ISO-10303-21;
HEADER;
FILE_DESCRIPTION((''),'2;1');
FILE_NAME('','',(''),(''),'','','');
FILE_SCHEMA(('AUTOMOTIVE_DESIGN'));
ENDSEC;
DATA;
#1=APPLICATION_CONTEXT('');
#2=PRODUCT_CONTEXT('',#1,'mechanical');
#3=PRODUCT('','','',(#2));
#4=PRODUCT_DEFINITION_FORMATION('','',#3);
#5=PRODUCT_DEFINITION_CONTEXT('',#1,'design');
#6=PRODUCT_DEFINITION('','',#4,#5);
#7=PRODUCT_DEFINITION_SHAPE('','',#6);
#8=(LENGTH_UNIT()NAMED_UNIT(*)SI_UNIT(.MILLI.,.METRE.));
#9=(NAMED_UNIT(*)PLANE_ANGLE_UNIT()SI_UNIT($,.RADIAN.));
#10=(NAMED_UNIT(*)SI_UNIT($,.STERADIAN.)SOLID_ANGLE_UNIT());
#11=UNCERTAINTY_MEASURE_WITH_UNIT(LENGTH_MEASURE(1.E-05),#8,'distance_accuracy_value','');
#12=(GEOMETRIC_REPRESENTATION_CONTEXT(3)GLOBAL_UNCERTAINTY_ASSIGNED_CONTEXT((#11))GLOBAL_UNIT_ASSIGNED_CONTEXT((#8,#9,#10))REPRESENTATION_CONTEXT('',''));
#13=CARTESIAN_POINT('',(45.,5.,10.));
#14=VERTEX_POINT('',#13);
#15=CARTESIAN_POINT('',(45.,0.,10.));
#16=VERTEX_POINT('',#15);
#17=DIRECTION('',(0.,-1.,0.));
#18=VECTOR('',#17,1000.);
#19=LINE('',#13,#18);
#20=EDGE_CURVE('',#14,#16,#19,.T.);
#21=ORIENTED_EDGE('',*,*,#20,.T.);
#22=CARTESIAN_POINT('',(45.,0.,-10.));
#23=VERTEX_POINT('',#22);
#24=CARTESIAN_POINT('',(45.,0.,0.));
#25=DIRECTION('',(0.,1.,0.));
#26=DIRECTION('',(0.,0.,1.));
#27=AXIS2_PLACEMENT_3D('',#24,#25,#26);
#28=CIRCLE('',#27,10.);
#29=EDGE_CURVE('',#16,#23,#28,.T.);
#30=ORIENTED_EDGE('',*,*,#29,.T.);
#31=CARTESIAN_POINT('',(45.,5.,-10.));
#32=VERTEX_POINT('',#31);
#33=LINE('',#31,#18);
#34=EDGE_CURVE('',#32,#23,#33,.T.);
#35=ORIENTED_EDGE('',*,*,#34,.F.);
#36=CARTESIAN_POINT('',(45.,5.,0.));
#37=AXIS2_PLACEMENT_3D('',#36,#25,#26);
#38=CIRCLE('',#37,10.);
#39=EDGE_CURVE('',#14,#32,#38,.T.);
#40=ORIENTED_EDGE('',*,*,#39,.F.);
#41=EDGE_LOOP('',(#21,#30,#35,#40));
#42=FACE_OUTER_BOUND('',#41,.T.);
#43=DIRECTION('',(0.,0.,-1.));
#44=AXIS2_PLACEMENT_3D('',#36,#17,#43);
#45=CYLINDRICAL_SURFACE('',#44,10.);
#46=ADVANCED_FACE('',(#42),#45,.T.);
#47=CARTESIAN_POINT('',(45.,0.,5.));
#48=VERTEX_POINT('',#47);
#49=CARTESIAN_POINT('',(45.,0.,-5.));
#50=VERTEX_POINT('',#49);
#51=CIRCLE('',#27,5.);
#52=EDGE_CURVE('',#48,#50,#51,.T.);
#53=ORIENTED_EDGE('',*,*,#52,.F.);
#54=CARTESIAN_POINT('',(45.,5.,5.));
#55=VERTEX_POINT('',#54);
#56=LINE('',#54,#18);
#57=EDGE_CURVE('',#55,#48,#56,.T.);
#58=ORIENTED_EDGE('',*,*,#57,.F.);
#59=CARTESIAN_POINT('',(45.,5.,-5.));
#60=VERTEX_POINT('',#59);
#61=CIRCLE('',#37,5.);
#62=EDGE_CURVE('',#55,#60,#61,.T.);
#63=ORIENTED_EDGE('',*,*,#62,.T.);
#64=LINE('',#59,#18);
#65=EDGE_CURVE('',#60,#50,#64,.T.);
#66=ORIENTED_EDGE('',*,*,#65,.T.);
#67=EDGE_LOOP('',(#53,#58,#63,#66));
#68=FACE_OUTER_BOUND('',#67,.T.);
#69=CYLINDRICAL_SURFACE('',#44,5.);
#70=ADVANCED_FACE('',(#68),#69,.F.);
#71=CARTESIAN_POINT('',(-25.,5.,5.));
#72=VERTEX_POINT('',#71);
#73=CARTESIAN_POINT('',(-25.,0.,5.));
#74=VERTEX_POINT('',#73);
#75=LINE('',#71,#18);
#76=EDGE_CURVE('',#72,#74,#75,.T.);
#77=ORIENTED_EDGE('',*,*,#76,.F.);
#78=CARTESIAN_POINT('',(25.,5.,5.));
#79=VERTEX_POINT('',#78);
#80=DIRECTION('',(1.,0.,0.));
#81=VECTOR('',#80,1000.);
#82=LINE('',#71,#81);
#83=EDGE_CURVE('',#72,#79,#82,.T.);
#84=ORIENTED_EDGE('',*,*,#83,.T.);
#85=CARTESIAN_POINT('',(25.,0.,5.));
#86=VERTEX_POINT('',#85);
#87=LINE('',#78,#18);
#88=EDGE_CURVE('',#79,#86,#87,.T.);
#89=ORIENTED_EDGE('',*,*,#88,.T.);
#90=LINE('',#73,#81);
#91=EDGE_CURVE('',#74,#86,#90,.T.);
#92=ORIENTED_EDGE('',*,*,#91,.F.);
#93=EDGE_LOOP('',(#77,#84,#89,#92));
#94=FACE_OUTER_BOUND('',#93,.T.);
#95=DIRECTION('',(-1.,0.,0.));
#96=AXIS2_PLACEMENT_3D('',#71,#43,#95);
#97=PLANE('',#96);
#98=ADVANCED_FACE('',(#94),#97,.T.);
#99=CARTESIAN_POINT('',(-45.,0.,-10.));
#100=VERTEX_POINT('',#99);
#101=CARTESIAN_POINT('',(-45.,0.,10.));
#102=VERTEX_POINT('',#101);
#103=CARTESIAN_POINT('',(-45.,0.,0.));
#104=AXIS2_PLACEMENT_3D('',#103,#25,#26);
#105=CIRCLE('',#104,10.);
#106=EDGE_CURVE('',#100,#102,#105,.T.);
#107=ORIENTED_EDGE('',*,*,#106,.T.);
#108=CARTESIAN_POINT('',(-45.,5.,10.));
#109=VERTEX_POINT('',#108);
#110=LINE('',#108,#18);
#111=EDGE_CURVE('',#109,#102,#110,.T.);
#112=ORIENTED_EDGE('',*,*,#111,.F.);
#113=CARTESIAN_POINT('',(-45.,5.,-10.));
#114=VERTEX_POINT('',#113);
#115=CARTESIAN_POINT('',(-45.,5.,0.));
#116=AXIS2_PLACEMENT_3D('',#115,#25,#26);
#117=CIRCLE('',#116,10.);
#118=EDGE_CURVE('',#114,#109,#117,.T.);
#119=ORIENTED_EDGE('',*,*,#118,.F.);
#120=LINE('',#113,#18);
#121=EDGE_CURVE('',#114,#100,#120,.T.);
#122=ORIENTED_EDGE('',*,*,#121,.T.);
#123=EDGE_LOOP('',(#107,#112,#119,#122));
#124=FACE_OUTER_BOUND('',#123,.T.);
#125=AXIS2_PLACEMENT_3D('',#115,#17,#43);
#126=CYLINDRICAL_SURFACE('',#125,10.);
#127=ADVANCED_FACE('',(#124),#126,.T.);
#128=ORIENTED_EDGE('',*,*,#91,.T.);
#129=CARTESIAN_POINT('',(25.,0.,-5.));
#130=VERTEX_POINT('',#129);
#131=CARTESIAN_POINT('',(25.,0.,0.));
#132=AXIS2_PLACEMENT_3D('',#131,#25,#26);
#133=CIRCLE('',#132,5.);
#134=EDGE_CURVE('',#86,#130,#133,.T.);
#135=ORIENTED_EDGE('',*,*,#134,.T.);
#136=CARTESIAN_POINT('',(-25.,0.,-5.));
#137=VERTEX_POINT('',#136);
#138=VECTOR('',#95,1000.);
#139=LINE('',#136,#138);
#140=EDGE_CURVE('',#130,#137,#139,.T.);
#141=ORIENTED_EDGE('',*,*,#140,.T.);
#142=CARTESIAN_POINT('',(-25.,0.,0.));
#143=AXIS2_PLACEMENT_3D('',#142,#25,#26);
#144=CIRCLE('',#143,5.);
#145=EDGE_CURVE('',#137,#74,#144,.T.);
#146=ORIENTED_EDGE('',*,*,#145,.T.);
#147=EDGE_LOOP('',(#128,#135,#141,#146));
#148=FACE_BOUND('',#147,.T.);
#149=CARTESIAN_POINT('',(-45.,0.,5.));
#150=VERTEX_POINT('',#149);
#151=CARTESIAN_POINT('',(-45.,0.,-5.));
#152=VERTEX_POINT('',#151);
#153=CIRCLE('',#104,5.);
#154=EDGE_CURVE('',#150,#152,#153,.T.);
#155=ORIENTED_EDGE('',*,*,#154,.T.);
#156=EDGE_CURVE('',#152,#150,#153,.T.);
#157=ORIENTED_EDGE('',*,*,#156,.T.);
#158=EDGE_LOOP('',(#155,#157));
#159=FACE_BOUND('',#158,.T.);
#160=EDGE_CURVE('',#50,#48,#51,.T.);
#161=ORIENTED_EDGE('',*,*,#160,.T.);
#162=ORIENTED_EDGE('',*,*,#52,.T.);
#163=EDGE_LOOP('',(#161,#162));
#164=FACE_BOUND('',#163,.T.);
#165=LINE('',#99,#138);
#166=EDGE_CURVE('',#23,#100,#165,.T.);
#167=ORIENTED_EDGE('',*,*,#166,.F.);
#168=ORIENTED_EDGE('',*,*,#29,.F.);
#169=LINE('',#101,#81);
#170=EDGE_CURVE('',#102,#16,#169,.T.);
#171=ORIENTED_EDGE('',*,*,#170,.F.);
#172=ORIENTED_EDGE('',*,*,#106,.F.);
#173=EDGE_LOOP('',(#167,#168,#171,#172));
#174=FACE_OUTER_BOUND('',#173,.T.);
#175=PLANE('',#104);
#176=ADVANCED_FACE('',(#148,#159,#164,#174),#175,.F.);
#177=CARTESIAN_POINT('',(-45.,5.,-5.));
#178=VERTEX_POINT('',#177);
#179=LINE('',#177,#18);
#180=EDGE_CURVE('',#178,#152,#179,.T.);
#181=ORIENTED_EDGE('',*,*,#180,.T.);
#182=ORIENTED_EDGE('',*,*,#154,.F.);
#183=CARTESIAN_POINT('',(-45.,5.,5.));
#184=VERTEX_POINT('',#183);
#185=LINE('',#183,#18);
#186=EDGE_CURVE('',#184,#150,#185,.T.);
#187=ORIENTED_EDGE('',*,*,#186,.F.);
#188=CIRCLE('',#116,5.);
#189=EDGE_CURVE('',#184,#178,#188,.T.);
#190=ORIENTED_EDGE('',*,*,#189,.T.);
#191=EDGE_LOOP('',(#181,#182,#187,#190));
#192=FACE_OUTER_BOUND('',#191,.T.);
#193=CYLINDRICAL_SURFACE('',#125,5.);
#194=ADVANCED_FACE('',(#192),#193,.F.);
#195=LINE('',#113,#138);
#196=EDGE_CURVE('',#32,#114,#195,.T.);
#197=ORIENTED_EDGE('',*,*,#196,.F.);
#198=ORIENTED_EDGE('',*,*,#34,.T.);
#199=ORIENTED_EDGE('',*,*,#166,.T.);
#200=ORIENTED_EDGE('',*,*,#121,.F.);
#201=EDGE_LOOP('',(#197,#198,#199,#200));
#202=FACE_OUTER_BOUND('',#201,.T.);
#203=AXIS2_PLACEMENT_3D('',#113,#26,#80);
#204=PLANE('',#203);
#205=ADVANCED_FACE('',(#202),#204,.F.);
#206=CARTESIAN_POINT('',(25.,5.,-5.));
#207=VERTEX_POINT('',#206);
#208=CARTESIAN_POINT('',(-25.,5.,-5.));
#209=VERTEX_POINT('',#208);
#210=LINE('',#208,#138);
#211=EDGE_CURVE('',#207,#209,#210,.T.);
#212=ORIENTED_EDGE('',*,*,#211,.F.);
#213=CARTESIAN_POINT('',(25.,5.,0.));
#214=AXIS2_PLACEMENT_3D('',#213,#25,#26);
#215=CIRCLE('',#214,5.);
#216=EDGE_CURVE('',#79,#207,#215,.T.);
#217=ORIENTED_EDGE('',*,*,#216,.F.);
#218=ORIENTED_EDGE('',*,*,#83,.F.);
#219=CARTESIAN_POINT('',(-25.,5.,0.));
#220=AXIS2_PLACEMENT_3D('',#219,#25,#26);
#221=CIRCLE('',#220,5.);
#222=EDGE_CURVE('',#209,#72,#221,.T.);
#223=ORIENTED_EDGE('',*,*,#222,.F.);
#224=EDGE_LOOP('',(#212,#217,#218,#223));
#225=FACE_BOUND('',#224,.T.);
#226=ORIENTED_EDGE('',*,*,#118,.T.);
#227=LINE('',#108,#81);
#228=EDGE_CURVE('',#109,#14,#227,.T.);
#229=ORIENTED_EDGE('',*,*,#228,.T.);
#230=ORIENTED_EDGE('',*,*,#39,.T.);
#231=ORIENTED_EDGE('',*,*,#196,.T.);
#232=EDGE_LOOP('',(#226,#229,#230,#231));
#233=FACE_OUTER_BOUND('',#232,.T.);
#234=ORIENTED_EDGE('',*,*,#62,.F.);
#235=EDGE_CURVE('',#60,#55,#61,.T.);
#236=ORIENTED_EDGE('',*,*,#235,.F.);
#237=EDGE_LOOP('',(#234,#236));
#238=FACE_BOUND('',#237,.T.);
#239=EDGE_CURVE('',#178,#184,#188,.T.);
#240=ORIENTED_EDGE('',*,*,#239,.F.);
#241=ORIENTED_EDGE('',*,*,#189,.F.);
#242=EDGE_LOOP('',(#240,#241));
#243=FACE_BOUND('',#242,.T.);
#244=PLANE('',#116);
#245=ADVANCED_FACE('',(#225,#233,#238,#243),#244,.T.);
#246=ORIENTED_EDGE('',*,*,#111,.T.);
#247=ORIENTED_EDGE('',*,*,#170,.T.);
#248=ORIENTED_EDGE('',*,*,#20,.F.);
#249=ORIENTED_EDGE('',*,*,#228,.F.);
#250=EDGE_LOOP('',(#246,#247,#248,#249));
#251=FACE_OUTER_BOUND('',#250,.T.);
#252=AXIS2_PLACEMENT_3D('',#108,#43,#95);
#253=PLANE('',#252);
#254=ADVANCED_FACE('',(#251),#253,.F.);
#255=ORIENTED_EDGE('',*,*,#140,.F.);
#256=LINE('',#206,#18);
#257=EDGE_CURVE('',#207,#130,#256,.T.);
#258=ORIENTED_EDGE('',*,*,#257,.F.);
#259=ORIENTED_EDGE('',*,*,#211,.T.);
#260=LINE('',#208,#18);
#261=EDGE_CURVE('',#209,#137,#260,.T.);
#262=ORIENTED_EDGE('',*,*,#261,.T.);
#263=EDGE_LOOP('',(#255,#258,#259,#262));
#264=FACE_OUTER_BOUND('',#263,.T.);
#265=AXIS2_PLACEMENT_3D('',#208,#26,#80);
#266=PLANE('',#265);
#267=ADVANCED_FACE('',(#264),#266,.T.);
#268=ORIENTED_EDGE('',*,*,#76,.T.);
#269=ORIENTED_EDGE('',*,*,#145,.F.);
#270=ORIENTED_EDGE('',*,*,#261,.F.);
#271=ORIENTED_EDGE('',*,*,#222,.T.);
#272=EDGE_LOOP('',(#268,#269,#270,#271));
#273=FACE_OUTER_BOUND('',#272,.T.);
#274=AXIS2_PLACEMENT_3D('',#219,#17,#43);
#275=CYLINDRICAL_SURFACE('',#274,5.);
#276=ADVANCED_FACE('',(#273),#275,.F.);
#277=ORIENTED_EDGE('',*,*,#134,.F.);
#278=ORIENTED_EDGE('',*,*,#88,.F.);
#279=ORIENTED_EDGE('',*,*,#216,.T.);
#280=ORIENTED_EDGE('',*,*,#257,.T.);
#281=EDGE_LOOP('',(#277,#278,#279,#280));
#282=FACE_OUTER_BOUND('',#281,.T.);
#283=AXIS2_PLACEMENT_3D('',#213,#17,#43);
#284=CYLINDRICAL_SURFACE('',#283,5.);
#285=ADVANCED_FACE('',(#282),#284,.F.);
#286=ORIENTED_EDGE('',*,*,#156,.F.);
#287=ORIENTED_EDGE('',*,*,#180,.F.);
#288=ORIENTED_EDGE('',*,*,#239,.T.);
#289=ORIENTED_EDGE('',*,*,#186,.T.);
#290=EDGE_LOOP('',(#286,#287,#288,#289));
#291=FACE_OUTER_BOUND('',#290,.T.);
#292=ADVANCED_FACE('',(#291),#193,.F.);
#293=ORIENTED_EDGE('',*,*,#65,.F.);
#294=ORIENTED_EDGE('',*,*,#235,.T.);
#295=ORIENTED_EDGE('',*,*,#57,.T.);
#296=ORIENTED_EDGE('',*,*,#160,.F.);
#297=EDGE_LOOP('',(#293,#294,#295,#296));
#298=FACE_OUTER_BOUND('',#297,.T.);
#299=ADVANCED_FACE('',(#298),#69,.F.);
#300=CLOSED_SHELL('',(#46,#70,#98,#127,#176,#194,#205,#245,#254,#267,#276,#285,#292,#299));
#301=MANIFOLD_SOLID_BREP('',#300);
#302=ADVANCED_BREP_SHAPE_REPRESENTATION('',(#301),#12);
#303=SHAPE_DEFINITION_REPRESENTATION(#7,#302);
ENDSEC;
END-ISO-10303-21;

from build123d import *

# Parameters (mm, degrees)
LINK_PROFILE_SKETCH_R = 5
LINK_PLATE_5MM_DEPTH  = 5


with BuildPart() as part:
    # Link Profile Sketch → Link Plate 5mm (new body)
    with BuildSketch(Plane(origin=(0, 0, 0), x_dir=(1, 0, 0), z_dir=(0, 1, 0))):
        with BuildLine():
            Line((-45, 10), (45, 10))
            ThreePointArc((45, 10), (55, 0), (45, -10))
            Line((45, -10), (-45, -10))
            ThreePointArc((-45, -10), (-55, 0), (-45, 10))
        make_face()
        with Locations(Location((-45, 0, 0), (0, 0, 270))):
            Circle(LINK_PROFILE_SKETCH_R, mode=Mode.SUBTRACT)
        with Locations(Location((45, 0, 0), (0, 0, 270))):
            Circle(LINK_PROFILE_SKETCH_R, mode=Mode.SUBTRACT)
        with BuildLine():
            Line((-25, 5), (25, 5))
            ThreePointArc((25, 5), (30, 0), (25, -5))
            Line((25, -5), (-25, -5))
            ThreePointArc((-25, -5), (-30, 0), (-25, 5))
        make_face(mode=Mode.SUBTRACT)
    extrude(amount=LINK_PLATE_5MM_DEPTH)


solid = part.part
